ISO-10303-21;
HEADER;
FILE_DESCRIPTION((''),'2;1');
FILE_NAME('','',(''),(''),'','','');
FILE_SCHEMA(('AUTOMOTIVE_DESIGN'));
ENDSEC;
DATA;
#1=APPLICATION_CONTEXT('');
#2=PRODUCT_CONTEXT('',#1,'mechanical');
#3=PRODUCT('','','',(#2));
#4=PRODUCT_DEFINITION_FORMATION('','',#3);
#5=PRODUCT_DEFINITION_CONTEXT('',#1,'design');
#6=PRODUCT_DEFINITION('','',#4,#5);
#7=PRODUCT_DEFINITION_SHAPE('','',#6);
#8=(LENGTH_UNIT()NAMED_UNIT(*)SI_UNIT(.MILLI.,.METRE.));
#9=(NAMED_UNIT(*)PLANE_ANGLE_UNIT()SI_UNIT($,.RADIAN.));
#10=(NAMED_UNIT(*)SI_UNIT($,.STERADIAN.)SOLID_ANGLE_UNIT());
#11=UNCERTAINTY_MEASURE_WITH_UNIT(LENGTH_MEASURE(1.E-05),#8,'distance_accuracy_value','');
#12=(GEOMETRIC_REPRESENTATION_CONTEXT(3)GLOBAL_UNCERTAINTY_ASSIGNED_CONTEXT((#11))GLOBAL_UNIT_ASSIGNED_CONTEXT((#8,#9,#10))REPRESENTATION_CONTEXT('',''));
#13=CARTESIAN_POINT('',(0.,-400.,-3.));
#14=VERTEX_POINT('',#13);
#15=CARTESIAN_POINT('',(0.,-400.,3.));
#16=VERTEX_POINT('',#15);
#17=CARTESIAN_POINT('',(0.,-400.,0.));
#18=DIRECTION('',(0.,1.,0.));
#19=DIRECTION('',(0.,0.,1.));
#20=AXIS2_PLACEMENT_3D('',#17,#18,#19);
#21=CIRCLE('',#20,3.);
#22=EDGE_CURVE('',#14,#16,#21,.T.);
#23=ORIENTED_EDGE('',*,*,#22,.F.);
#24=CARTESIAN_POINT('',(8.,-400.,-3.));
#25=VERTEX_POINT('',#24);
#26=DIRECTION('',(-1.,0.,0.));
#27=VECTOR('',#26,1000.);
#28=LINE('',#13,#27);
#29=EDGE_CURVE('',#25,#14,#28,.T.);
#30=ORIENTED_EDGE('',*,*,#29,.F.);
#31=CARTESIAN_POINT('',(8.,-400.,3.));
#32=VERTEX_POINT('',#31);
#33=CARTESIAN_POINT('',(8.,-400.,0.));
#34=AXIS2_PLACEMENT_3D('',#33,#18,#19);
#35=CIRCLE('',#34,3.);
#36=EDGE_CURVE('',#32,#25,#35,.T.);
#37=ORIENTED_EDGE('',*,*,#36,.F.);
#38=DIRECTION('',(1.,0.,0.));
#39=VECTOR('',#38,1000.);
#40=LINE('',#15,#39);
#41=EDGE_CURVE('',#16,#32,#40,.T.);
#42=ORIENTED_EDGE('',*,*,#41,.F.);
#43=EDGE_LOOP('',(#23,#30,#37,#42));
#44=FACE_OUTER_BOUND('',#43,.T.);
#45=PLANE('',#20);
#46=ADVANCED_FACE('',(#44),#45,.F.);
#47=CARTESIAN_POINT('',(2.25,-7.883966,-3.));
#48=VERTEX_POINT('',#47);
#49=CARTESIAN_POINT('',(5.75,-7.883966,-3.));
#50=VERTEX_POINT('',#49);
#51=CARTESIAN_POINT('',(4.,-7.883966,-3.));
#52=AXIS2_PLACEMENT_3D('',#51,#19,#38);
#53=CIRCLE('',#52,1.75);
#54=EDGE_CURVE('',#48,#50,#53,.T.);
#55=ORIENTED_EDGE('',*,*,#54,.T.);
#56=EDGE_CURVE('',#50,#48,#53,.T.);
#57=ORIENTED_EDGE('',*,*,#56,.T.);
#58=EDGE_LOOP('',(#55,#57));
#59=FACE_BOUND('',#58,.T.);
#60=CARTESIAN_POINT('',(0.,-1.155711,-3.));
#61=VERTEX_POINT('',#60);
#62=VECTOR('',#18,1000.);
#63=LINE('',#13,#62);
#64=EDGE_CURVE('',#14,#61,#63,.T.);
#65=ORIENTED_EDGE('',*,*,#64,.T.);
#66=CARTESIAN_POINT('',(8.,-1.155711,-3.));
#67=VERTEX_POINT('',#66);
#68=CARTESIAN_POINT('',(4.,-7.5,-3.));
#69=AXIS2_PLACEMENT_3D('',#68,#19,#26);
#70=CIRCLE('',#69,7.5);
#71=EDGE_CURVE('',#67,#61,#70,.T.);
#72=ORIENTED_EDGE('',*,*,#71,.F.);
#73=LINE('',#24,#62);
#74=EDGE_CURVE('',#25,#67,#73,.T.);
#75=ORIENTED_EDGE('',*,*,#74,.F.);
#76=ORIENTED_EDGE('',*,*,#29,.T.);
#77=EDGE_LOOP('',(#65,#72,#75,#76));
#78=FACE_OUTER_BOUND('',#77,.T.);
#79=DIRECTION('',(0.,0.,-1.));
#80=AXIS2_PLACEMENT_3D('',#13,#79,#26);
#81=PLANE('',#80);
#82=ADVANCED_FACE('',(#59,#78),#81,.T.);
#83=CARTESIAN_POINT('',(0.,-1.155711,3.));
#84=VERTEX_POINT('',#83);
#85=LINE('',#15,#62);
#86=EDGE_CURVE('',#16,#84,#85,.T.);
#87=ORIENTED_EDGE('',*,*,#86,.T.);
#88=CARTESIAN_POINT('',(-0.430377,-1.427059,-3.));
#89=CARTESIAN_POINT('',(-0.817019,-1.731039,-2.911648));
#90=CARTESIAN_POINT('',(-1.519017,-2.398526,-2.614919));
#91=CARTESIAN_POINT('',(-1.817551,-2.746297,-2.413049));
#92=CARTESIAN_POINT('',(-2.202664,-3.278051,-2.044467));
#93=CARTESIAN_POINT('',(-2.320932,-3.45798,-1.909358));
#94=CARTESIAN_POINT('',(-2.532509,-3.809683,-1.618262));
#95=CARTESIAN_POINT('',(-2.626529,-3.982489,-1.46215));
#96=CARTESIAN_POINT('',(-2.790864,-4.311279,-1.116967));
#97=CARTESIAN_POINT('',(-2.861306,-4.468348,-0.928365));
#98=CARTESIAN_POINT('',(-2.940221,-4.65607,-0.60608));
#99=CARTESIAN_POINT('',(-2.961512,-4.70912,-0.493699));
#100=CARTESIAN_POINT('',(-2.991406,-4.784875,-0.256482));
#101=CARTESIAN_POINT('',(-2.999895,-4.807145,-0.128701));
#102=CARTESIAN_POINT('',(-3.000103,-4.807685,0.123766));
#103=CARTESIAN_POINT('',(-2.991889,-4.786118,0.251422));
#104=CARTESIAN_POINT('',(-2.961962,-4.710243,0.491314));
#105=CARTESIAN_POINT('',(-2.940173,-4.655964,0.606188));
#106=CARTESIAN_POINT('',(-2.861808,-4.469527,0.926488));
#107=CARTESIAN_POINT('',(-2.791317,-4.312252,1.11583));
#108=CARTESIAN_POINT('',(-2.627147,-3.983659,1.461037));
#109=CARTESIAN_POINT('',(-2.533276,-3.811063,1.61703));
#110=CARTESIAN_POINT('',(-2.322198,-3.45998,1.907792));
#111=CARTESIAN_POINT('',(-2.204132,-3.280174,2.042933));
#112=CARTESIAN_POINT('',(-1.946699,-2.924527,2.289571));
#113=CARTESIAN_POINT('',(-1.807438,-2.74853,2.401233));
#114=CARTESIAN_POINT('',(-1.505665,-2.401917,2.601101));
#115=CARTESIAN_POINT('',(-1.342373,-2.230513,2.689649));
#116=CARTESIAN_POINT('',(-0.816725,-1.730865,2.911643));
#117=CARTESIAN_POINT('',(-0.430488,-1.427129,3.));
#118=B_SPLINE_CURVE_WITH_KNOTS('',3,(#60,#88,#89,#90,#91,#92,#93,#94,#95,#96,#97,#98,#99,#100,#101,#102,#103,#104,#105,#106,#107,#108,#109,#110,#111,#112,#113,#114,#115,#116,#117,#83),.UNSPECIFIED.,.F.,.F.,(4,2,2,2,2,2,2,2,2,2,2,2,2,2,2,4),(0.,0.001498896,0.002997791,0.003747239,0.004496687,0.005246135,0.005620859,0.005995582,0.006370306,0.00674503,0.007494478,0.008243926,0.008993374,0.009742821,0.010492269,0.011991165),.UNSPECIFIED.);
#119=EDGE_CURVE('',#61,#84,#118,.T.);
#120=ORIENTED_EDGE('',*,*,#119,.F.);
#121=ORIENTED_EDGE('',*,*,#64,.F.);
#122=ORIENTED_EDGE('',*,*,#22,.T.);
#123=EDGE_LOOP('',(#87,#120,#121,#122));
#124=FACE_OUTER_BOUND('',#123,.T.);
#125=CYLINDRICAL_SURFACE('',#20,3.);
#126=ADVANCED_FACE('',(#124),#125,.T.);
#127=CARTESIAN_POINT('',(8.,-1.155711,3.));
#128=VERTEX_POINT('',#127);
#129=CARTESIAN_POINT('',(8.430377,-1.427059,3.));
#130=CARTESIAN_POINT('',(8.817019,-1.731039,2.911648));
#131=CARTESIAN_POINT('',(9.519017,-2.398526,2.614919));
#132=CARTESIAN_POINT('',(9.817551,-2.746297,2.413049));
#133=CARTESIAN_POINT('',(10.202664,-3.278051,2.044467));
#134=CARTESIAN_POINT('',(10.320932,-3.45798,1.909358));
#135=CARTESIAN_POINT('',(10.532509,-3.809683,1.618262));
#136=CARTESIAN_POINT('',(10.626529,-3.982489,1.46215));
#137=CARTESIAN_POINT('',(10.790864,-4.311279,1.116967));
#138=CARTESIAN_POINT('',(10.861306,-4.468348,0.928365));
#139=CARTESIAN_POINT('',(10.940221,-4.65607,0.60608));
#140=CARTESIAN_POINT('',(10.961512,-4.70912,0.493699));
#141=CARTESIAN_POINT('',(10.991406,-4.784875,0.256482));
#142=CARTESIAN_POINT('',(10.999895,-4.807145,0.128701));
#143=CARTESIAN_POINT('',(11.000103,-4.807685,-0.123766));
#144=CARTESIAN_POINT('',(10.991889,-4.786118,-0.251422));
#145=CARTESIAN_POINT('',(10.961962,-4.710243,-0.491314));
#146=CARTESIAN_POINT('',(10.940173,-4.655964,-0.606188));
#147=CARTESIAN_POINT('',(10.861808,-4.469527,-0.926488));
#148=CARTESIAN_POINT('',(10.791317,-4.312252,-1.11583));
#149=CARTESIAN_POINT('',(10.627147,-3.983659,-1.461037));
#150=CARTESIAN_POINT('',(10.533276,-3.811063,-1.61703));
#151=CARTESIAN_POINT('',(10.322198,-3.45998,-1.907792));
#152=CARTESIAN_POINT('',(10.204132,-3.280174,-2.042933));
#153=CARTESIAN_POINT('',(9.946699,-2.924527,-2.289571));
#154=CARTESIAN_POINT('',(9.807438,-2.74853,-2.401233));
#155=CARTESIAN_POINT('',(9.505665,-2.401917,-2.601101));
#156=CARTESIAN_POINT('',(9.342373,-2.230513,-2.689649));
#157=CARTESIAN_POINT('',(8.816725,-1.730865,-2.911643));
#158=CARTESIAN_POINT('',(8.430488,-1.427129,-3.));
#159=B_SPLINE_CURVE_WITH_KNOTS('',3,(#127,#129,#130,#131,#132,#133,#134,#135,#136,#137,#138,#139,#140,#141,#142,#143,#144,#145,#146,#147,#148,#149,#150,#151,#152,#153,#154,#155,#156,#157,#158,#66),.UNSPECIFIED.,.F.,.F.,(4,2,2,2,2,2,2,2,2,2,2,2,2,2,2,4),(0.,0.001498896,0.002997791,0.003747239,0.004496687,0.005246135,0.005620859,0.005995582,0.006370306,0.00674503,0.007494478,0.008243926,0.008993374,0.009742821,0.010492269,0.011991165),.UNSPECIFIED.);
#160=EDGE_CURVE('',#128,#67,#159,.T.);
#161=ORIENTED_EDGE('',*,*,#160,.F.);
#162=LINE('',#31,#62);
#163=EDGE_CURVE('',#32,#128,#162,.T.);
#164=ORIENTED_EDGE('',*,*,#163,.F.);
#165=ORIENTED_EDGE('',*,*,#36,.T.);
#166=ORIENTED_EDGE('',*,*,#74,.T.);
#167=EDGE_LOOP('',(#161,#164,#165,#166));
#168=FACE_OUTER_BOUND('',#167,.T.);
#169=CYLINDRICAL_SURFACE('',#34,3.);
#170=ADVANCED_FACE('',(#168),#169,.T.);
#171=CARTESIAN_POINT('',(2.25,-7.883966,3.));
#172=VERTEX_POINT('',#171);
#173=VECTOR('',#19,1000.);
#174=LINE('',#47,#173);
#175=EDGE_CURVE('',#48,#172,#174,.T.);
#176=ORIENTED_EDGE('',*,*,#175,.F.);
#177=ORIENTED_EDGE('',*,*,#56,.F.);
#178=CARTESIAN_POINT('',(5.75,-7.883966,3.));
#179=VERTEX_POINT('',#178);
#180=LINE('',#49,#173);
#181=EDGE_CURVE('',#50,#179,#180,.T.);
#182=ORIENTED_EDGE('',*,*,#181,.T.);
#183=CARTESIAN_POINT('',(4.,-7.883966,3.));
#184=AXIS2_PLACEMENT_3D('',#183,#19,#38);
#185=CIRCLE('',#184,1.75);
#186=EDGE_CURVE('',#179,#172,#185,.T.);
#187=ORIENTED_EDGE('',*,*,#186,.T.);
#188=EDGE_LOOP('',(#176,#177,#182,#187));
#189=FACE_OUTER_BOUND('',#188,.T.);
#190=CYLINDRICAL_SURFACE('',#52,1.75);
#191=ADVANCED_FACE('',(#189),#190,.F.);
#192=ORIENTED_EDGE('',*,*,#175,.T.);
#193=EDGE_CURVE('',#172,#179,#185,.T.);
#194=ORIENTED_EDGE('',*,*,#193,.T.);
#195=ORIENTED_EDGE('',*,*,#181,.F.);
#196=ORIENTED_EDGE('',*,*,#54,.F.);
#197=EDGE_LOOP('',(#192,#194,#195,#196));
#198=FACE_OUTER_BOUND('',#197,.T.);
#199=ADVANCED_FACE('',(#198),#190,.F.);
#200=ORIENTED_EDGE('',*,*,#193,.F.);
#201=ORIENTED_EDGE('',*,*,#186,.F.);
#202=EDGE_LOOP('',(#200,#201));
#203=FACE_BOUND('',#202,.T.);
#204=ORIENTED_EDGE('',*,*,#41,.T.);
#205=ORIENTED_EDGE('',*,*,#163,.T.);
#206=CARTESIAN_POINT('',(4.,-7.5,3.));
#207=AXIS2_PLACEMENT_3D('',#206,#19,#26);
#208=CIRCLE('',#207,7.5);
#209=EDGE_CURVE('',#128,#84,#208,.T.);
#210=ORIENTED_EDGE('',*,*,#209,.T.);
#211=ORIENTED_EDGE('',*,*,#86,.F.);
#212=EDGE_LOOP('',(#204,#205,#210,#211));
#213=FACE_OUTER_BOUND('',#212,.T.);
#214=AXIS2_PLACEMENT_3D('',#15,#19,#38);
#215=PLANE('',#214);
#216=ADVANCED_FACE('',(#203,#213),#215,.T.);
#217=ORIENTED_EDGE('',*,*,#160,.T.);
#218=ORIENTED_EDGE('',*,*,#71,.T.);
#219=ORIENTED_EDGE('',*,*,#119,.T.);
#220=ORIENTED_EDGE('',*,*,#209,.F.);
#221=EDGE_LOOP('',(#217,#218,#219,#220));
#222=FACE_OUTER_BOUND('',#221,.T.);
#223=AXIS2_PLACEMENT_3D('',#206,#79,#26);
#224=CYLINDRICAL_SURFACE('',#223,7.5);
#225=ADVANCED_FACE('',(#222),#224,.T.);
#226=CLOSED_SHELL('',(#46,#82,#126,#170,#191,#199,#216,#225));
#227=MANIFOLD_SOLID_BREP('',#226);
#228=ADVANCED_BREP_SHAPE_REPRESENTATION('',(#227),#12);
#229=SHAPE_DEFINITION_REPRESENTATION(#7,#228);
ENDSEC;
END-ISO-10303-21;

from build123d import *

# Parameters (mm, degrees)
BOSS_EXTRUDE1_DEPTH = 400
CUT_EXTRUDE1_DEPTH  = 401.196201881
SKETCH3_R           = 1.75
CUT_EXTRUDE2_DEPTH  = 401.196201985


with BuildPart() as part:
    # Sketch1 → Boss-Extrude1 (new body)
    with BuildSketch(Plane(origin=(0, 0, 0), x_dir=(1, 0, 0), z_dir=(0, 1, 0))):
        with BuildLine():
            Line((0, 3), (8, 3))
            ThreePointArc((8, 3), (11, 0), (8, -3))
            Line((8, -3), (0, -3))
            ThreePointArc((0, -3), (-3, 0), (0, 3))
        make_face()
    extrude(amount=-BOSS_EXTRUDE1_DEPTH)

    # Sketch2 → Cut-Extrude1 (cut, through all)
    with BuildSketch(Plane(origin=(0, 0, -3), x_dir=(-1, 0, 0), z_dir=(0, 0, -1))):
        with BuildLine():
            Line((9.595782006, 3.055219164), (9.595782006, -10.123279697))
            Line((9.595782006, -10.123279697), (3.026265269, -10.123279697))
            ThreePointArc((3.026265269, -10.123279697), (-4, 0), (-11.026265269, -10.123279697))
            Line((-11.026265269, -10.123279697), (-18.139014199, -10.123279697))
            Line((-18.139014199, -10.123279697), (-18.139014199, 3.055219164))
            Line((-18.139014199, 3.055219164), (9.595782006, 3.055219164))
        make_face()
    extrude(amount=-CUT_EXTRUDE1_DEPTH, mode=Mode.SUBTRACT)

    # Sketch3 → Cut-Extrude2 (cut, through all)
    with BuildSketch(Plane.XY.offset(3)):
        with Locations((4, -7.883965637)):
            Circle(SKETCH3_R)
    extrude(amount=-CUT_EXTRUDE2_DEPTH, mode=Mode.SUBTRACT)


solid = part.part
